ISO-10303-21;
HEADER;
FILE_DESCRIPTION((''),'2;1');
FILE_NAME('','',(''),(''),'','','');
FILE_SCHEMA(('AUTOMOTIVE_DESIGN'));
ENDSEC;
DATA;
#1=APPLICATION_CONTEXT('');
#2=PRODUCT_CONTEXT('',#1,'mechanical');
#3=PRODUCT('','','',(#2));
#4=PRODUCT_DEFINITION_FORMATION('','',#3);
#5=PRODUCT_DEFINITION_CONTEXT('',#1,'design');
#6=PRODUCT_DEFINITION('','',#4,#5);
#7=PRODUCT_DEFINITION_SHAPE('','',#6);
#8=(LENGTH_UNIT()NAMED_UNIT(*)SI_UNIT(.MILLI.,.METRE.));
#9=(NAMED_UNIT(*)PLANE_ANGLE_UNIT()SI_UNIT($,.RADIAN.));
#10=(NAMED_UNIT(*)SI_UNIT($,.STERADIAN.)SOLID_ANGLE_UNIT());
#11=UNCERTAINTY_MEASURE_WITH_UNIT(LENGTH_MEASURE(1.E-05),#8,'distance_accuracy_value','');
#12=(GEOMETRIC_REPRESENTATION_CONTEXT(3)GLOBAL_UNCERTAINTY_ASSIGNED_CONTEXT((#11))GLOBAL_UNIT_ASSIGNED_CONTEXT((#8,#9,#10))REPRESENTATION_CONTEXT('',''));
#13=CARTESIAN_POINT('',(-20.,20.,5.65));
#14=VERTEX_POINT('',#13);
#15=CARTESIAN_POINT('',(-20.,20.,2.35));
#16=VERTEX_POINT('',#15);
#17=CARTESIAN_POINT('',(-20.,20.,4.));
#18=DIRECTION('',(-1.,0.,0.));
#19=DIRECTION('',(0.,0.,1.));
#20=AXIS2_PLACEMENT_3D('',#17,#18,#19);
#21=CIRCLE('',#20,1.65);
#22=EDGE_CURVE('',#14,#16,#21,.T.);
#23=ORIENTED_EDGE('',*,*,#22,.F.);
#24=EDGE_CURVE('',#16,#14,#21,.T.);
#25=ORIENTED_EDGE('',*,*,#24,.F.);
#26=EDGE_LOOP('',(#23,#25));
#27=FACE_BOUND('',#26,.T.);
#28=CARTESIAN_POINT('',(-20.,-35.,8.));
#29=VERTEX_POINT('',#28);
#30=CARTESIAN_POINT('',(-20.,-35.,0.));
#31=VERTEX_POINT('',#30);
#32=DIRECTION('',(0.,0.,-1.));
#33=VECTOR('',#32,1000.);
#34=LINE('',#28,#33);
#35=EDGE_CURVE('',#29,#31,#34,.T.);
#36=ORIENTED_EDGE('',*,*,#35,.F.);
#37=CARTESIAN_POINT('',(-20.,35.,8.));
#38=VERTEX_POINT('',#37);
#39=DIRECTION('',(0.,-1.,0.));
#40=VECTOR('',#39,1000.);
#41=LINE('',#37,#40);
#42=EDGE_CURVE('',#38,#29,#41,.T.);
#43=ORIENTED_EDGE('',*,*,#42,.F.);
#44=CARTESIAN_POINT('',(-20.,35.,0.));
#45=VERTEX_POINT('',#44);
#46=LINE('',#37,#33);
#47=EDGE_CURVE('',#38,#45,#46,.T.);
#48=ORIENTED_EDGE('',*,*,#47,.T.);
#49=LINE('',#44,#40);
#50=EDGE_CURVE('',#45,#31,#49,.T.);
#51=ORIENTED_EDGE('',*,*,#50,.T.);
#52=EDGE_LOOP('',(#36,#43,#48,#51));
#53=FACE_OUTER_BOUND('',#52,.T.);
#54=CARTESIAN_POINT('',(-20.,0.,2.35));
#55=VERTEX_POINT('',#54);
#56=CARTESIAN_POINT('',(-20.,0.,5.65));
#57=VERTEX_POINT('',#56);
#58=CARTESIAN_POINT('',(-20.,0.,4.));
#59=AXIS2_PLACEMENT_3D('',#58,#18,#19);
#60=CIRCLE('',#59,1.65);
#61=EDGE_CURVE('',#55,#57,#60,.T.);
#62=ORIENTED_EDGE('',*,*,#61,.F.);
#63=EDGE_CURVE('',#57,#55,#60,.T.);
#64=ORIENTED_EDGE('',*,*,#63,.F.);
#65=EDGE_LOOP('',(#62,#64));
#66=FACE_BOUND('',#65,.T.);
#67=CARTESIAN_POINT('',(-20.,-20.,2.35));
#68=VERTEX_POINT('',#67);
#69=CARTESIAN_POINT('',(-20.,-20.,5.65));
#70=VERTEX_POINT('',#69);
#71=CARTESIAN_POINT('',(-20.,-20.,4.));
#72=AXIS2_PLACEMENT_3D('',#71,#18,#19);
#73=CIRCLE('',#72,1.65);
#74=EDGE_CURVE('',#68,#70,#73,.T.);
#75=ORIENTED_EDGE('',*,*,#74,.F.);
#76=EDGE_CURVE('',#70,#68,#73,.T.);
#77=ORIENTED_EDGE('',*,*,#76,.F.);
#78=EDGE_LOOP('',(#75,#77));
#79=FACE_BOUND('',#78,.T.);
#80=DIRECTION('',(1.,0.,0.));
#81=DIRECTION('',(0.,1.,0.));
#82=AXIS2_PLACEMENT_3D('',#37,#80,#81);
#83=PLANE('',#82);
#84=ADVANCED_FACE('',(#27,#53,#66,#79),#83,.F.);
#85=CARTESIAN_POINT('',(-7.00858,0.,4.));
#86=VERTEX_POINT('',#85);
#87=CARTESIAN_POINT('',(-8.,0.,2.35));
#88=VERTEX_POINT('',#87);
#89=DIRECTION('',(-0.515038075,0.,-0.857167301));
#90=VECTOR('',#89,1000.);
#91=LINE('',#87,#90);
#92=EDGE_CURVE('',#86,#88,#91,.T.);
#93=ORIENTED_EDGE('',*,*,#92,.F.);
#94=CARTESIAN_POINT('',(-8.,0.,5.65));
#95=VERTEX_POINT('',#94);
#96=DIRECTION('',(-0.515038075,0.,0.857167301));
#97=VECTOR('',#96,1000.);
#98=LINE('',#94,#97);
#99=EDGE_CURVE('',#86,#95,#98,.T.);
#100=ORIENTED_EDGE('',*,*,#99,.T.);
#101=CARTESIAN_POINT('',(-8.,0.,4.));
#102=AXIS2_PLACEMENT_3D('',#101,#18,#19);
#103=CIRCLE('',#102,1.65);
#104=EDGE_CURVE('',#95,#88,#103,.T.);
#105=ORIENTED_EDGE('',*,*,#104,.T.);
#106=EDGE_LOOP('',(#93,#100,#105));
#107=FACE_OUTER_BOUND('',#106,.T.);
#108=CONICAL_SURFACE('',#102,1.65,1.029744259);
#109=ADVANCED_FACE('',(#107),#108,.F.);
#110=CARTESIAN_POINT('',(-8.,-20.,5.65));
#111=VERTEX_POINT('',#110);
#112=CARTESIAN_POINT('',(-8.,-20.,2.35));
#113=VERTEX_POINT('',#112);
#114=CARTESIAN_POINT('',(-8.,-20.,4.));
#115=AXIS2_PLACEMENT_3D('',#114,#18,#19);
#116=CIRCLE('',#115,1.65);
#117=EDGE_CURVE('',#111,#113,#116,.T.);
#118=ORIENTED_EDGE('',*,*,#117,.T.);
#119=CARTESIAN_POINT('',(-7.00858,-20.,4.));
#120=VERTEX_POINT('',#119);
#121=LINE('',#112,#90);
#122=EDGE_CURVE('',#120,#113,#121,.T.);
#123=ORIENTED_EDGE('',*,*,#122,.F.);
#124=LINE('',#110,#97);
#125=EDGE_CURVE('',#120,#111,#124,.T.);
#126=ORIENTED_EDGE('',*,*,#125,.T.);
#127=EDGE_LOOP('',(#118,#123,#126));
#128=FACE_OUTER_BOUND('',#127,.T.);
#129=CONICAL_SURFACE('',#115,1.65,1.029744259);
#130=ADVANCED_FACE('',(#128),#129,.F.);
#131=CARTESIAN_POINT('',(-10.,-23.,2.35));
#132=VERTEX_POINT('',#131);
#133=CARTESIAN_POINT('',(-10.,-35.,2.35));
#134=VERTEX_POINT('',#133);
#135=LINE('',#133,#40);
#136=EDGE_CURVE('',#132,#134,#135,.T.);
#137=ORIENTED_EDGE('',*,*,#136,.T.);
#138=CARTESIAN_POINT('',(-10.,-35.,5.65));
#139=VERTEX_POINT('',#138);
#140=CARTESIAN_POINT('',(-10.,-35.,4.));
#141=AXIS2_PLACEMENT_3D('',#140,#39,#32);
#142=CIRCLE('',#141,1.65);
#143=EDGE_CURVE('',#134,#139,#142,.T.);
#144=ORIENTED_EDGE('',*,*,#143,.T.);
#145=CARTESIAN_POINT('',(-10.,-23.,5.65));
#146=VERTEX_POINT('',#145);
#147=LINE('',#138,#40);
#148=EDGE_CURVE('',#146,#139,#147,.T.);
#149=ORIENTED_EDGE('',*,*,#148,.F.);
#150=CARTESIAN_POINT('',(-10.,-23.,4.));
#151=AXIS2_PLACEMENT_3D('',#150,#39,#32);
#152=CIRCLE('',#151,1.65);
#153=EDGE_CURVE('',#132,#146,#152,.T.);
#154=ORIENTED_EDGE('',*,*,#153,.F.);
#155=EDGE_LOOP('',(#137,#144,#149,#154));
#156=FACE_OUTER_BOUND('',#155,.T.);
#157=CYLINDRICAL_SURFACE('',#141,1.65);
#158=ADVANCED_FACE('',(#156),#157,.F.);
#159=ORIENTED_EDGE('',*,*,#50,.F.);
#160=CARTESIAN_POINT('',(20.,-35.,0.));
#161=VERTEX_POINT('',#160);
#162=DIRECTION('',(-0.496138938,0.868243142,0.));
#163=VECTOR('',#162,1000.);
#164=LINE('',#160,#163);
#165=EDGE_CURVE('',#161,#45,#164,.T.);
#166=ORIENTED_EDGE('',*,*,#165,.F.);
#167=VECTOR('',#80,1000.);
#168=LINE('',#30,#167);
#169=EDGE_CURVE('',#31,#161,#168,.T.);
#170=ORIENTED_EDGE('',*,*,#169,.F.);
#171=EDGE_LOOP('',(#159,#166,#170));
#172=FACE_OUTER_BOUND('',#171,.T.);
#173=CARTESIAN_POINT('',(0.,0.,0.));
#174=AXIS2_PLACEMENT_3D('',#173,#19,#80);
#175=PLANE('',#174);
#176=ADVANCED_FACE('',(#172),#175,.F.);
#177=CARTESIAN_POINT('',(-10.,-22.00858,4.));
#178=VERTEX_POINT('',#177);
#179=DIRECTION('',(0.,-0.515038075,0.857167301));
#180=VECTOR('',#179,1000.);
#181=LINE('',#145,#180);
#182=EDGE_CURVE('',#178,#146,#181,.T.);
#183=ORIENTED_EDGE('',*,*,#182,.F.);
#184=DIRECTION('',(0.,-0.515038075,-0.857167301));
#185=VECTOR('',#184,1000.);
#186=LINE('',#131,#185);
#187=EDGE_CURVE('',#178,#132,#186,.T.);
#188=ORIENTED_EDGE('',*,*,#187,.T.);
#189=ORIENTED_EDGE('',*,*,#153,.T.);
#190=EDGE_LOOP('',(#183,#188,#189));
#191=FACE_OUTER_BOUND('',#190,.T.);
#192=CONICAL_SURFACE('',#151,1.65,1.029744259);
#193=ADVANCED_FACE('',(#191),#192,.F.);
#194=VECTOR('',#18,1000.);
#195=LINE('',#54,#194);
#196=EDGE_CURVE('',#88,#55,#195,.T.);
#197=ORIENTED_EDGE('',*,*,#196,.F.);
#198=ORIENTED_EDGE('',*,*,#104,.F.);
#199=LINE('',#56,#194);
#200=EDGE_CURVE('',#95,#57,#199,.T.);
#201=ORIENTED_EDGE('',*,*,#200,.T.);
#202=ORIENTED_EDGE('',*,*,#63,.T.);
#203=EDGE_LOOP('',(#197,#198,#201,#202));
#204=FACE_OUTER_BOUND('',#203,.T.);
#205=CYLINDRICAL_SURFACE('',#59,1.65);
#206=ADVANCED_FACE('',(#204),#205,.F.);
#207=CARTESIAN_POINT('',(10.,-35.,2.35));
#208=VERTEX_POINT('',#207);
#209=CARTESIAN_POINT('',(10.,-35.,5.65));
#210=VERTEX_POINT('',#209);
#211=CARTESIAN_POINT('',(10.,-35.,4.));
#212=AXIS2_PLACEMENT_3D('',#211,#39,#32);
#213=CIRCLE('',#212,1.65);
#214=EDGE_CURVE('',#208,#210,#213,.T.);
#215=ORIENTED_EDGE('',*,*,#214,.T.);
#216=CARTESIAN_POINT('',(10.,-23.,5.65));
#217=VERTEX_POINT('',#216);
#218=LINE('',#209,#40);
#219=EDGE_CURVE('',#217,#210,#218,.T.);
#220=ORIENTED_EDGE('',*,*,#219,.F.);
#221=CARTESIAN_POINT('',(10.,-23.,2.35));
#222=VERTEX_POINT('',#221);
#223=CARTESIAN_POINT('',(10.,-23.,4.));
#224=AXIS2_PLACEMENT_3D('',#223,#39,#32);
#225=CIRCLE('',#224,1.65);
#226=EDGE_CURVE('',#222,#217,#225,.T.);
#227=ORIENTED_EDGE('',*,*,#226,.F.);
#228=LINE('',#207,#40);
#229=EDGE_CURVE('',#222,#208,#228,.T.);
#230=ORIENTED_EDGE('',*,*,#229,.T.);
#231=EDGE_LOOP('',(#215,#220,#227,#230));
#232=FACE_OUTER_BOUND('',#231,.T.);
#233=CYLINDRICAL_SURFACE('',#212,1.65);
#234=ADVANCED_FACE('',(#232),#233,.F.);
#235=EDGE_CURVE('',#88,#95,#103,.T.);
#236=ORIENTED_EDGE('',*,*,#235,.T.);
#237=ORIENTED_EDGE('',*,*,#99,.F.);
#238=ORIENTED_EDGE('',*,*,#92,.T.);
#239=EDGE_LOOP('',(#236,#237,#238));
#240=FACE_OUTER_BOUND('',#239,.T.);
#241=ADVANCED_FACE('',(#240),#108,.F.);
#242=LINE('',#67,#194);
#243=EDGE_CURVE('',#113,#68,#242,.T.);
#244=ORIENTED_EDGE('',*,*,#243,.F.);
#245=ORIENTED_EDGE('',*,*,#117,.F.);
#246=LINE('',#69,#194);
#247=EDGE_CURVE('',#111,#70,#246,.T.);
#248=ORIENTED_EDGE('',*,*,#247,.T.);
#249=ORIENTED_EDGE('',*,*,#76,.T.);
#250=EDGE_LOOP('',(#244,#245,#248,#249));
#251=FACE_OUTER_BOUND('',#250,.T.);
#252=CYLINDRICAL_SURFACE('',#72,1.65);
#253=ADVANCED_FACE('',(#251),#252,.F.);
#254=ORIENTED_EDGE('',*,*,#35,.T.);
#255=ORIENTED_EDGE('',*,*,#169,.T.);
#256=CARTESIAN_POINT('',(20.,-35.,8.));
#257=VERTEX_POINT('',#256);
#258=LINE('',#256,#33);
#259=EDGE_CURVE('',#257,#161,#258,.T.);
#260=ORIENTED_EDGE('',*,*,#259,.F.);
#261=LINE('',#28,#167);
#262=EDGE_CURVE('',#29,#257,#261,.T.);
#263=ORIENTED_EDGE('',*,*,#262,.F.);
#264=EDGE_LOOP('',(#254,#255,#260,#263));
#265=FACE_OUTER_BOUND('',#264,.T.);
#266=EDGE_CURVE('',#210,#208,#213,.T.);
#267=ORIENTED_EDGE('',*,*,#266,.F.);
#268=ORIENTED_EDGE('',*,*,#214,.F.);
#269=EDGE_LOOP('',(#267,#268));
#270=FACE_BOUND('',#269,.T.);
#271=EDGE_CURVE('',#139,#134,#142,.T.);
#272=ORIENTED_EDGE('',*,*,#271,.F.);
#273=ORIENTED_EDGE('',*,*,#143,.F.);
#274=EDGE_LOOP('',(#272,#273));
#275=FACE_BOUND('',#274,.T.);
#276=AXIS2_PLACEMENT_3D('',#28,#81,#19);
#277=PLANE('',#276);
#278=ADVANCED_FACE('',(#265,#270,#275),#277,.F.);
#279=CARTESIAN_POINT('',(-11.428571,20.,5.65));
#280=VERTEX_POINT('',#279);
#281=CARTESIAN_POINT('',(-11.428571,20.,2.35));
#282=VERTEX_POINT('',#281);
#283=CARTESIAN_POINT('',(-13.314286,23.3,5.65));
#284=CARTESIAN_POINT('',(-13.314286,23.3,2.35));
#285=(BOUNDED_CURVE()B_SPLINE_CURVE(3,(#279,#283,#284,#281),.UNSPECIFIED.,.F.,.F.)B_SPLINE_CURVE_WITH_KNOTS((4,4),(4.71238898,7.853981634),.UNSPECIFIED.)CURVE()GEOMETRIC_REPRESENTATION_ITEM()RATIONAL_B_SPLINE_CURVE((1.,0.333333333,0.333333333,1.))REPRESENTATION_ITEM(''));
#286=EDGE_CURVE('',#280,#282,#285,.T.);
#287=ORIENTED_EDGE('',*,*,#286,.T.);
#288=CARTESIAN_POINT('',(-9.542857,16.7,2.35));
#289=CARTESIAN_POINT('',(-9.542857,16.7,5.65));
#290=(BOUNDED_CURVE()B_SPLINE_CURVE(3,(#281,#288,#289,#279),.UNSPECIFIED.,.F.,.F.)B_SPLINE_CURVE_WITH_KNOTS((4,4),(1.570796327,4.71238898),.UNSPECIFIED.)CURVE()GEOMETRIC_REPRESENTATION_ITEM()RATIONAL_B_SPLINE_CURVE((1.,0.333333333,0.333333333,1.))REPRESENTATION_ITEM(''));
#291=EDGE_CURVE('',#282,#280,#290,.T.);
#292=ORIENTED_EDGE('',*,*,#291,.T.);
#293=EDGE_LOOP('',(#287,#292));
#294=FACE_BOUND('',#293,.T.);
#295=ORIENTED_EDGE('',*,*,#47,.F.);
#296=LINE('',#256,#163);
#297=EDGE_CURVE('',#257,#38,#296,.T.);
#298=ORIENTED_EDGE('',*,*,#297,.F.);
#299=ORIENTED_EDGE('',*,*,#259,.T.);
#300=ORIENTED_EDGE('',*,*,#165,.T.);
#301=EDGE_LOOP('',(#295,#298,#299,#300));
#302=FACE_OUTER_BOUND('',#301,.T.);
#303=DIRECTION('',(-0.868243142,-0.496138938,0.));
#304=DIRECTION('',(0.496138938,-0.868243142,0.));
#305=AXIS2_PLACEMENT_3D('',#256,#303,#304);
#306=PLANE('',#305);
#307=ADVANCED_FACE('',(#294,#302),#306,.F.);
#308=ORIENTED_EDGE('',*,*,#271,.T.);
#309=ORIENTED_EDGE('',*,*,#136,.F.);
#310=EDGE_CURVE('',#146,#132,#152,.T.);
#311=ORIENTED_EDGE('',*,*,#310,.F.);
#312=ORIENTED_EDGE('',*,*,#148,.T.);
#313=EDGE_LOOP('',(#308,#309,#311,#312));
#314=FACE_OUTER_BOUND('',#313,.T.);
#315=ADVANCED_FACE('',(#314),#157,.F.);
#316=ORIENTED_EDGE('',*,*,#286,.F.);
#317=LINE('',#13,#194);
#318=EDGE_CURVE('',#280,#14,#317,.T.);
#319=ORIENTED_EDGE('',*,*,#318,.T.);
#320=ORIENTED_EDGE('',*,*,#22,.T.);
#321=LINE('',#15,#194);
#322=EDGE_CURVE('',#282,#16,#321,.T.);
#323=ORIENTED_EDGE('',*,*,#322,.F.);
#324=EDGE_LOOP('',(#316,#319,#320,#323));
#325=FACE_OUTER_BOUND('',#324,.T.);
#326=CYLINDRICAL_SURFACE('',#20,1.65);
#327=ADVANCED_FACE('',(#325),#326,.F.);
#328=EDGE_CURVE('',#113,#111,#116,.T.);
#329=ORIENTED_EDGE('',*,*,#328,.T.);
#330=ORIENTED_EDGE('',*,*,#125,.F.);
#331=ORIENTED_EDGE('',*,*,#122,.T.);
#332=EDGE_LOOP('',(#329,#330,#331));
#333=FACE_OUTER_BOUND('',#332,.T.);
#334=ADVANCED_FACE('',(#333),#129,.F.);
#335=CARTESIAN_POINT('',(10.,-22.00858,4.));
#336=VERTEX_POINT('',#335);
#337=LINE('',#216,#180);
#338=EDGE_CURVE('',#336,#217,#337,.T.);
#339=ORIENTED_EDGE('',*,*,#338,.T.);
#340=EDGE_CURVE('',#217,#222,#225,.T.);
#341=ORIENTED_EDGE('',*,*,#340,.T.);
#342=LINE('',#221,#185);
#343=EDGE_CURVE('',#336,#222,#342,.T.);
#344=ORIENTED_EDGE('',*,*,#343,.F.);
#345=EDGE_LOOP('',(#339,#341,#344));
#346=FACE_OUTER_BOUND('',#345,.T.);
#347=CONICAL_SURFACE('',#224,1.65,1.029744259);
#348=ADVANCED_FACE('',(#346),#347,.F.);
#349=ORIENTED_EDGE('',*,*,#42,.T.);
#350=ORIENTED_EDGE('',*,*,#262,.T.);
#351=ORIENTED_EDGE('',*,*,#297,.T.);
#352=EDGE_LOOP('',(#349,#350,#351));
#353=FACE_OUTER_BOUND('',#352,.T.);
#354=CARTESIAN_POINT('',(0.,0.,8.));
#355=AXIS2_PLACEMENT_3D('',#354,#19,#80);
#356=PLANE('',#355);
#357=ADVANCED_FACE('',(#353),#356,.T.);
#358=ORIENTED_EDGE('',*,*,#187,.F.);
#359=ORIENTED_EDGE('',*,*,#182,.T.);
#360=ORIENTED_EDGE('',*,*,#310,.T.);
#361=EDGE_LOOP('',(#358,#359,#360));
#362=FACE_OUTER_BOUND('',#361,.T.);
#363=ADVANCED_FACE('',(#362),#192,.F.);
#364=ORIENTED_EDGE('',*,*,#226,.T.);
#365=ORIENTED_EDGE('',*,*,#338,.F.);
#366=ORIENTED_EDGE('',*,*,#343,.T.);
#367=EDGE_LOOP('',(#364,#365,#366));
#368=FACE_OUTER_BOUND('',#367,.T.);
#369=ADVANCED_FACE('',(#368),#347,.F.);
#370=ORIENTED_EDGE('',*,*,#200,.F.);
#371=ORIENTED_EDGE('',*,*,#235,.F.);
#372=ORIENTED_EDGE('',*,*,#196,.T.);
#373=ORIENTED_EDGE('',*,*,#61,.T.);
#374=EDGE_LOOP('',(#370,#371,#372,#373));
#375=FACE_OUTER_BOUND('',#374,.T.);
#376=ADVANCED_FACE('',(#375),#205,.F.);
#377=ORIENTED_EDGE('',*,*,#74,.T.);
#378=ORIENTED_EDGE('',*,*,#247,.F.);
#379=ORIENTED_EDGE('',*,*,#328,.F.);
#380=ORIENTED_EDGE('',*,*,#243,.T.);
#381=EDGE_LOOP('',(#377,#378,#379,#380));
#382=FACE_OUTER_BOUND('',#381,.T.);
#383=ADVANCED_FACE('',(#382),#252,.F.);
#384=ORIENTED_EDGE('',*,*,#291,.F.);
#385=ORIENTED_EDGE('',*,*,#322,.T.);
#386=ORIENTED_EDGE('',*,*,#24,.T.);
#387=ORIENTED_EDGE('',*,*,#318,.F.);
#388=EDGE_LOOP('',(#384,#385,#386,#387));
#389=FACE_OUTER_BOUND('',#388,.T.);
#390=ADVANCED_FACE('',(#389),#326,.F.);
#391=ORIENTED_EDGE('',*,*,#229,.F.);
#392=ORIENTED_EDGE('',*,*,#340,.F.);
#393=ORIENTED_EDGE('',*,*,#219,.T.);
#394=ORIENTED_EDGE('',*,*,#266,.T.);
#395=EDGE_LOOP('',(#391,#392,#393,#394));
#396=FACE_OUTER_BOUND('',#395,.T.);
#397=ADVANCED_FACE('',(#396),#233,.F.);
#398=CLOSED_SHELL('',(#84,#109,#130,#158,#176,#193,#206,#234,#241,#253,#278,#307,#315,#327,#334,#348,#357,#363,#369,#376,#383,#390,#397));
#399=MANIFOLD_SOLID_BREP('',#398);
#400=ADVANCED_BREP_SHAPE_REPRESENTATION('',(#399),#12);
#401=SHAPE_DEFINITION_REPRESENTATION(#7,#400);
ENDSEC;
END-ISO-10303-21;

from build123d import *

# Parameters (mm, degrees)
EXTRUDE_1_DEPTH        = 8
HOLE_WIZARD_M4_1_D     = 3.3
HOLE_WIZARD_M4_1_DEPTH = 12
HOLE_WIZARD_M4_1_TIP   = 0.991420021
HOLE_WIZARD_M4_2_D     = 3.3
HOLE_WIZARD_M4_2_DEPTH = 12
HOLE_WIZARD_M4_2_TIP   = 0.991420021


with BuildPart() as part:
    # 草图1 → 凸台-拉伸1 (new body)
    with BuildSketch(Plane.XY):
        Polygon((-20, -35), (20, -35), (-20, 35), align=None)
    extrude(amount=EXTRUDE_1_DEPTH)

    # M4 螺纹孔1
    with Locations(Plane.ZY.offset(20)):
        with Locations((4, -20), (4, 0), (4, 20)):
            Hole(HOLE_WIZARD_M4_1_D / 2, depth=HOLE_WIZARD_M4_1_DEPTH)
            with Locations((0, 0, -(HOLE_WIZARD_M4_1_DEPTH + HOLE_WIZARD_M4_1_TIP / 2))):  # 118° drill point
                Cone(0, HOLE_WIZARD_M4_1_D / 2, HOLE_WIZARD_M4_1_TIP, mode=Mode.SUBTRACT)

    # M4 螺纹孔2
    with Locations(Plane(origin=(0, -35, 0), x_dir=(-1, 0, 0), z_dir=(0, -1, 0))):
        with Locations((-10, -4), (10, -4)):
            Hole(HOLE_WIZARD_M4_2_D / 2, depth=HOLE_WIZARD_M4_2_DEPTH)
            with Locations((0, 0, -(HOLE_WIZARD_M4_2_DEPTH + HOLE_WIZARD_M4_2_TIP / 2))):  # 118° drill point
                Cone(0, HOLE_WIZARD_M4_2_D / 2, HOLE_WIZARD_M4_2_TIP, mode=Mode.SUBTRACT)


solid = part.part
